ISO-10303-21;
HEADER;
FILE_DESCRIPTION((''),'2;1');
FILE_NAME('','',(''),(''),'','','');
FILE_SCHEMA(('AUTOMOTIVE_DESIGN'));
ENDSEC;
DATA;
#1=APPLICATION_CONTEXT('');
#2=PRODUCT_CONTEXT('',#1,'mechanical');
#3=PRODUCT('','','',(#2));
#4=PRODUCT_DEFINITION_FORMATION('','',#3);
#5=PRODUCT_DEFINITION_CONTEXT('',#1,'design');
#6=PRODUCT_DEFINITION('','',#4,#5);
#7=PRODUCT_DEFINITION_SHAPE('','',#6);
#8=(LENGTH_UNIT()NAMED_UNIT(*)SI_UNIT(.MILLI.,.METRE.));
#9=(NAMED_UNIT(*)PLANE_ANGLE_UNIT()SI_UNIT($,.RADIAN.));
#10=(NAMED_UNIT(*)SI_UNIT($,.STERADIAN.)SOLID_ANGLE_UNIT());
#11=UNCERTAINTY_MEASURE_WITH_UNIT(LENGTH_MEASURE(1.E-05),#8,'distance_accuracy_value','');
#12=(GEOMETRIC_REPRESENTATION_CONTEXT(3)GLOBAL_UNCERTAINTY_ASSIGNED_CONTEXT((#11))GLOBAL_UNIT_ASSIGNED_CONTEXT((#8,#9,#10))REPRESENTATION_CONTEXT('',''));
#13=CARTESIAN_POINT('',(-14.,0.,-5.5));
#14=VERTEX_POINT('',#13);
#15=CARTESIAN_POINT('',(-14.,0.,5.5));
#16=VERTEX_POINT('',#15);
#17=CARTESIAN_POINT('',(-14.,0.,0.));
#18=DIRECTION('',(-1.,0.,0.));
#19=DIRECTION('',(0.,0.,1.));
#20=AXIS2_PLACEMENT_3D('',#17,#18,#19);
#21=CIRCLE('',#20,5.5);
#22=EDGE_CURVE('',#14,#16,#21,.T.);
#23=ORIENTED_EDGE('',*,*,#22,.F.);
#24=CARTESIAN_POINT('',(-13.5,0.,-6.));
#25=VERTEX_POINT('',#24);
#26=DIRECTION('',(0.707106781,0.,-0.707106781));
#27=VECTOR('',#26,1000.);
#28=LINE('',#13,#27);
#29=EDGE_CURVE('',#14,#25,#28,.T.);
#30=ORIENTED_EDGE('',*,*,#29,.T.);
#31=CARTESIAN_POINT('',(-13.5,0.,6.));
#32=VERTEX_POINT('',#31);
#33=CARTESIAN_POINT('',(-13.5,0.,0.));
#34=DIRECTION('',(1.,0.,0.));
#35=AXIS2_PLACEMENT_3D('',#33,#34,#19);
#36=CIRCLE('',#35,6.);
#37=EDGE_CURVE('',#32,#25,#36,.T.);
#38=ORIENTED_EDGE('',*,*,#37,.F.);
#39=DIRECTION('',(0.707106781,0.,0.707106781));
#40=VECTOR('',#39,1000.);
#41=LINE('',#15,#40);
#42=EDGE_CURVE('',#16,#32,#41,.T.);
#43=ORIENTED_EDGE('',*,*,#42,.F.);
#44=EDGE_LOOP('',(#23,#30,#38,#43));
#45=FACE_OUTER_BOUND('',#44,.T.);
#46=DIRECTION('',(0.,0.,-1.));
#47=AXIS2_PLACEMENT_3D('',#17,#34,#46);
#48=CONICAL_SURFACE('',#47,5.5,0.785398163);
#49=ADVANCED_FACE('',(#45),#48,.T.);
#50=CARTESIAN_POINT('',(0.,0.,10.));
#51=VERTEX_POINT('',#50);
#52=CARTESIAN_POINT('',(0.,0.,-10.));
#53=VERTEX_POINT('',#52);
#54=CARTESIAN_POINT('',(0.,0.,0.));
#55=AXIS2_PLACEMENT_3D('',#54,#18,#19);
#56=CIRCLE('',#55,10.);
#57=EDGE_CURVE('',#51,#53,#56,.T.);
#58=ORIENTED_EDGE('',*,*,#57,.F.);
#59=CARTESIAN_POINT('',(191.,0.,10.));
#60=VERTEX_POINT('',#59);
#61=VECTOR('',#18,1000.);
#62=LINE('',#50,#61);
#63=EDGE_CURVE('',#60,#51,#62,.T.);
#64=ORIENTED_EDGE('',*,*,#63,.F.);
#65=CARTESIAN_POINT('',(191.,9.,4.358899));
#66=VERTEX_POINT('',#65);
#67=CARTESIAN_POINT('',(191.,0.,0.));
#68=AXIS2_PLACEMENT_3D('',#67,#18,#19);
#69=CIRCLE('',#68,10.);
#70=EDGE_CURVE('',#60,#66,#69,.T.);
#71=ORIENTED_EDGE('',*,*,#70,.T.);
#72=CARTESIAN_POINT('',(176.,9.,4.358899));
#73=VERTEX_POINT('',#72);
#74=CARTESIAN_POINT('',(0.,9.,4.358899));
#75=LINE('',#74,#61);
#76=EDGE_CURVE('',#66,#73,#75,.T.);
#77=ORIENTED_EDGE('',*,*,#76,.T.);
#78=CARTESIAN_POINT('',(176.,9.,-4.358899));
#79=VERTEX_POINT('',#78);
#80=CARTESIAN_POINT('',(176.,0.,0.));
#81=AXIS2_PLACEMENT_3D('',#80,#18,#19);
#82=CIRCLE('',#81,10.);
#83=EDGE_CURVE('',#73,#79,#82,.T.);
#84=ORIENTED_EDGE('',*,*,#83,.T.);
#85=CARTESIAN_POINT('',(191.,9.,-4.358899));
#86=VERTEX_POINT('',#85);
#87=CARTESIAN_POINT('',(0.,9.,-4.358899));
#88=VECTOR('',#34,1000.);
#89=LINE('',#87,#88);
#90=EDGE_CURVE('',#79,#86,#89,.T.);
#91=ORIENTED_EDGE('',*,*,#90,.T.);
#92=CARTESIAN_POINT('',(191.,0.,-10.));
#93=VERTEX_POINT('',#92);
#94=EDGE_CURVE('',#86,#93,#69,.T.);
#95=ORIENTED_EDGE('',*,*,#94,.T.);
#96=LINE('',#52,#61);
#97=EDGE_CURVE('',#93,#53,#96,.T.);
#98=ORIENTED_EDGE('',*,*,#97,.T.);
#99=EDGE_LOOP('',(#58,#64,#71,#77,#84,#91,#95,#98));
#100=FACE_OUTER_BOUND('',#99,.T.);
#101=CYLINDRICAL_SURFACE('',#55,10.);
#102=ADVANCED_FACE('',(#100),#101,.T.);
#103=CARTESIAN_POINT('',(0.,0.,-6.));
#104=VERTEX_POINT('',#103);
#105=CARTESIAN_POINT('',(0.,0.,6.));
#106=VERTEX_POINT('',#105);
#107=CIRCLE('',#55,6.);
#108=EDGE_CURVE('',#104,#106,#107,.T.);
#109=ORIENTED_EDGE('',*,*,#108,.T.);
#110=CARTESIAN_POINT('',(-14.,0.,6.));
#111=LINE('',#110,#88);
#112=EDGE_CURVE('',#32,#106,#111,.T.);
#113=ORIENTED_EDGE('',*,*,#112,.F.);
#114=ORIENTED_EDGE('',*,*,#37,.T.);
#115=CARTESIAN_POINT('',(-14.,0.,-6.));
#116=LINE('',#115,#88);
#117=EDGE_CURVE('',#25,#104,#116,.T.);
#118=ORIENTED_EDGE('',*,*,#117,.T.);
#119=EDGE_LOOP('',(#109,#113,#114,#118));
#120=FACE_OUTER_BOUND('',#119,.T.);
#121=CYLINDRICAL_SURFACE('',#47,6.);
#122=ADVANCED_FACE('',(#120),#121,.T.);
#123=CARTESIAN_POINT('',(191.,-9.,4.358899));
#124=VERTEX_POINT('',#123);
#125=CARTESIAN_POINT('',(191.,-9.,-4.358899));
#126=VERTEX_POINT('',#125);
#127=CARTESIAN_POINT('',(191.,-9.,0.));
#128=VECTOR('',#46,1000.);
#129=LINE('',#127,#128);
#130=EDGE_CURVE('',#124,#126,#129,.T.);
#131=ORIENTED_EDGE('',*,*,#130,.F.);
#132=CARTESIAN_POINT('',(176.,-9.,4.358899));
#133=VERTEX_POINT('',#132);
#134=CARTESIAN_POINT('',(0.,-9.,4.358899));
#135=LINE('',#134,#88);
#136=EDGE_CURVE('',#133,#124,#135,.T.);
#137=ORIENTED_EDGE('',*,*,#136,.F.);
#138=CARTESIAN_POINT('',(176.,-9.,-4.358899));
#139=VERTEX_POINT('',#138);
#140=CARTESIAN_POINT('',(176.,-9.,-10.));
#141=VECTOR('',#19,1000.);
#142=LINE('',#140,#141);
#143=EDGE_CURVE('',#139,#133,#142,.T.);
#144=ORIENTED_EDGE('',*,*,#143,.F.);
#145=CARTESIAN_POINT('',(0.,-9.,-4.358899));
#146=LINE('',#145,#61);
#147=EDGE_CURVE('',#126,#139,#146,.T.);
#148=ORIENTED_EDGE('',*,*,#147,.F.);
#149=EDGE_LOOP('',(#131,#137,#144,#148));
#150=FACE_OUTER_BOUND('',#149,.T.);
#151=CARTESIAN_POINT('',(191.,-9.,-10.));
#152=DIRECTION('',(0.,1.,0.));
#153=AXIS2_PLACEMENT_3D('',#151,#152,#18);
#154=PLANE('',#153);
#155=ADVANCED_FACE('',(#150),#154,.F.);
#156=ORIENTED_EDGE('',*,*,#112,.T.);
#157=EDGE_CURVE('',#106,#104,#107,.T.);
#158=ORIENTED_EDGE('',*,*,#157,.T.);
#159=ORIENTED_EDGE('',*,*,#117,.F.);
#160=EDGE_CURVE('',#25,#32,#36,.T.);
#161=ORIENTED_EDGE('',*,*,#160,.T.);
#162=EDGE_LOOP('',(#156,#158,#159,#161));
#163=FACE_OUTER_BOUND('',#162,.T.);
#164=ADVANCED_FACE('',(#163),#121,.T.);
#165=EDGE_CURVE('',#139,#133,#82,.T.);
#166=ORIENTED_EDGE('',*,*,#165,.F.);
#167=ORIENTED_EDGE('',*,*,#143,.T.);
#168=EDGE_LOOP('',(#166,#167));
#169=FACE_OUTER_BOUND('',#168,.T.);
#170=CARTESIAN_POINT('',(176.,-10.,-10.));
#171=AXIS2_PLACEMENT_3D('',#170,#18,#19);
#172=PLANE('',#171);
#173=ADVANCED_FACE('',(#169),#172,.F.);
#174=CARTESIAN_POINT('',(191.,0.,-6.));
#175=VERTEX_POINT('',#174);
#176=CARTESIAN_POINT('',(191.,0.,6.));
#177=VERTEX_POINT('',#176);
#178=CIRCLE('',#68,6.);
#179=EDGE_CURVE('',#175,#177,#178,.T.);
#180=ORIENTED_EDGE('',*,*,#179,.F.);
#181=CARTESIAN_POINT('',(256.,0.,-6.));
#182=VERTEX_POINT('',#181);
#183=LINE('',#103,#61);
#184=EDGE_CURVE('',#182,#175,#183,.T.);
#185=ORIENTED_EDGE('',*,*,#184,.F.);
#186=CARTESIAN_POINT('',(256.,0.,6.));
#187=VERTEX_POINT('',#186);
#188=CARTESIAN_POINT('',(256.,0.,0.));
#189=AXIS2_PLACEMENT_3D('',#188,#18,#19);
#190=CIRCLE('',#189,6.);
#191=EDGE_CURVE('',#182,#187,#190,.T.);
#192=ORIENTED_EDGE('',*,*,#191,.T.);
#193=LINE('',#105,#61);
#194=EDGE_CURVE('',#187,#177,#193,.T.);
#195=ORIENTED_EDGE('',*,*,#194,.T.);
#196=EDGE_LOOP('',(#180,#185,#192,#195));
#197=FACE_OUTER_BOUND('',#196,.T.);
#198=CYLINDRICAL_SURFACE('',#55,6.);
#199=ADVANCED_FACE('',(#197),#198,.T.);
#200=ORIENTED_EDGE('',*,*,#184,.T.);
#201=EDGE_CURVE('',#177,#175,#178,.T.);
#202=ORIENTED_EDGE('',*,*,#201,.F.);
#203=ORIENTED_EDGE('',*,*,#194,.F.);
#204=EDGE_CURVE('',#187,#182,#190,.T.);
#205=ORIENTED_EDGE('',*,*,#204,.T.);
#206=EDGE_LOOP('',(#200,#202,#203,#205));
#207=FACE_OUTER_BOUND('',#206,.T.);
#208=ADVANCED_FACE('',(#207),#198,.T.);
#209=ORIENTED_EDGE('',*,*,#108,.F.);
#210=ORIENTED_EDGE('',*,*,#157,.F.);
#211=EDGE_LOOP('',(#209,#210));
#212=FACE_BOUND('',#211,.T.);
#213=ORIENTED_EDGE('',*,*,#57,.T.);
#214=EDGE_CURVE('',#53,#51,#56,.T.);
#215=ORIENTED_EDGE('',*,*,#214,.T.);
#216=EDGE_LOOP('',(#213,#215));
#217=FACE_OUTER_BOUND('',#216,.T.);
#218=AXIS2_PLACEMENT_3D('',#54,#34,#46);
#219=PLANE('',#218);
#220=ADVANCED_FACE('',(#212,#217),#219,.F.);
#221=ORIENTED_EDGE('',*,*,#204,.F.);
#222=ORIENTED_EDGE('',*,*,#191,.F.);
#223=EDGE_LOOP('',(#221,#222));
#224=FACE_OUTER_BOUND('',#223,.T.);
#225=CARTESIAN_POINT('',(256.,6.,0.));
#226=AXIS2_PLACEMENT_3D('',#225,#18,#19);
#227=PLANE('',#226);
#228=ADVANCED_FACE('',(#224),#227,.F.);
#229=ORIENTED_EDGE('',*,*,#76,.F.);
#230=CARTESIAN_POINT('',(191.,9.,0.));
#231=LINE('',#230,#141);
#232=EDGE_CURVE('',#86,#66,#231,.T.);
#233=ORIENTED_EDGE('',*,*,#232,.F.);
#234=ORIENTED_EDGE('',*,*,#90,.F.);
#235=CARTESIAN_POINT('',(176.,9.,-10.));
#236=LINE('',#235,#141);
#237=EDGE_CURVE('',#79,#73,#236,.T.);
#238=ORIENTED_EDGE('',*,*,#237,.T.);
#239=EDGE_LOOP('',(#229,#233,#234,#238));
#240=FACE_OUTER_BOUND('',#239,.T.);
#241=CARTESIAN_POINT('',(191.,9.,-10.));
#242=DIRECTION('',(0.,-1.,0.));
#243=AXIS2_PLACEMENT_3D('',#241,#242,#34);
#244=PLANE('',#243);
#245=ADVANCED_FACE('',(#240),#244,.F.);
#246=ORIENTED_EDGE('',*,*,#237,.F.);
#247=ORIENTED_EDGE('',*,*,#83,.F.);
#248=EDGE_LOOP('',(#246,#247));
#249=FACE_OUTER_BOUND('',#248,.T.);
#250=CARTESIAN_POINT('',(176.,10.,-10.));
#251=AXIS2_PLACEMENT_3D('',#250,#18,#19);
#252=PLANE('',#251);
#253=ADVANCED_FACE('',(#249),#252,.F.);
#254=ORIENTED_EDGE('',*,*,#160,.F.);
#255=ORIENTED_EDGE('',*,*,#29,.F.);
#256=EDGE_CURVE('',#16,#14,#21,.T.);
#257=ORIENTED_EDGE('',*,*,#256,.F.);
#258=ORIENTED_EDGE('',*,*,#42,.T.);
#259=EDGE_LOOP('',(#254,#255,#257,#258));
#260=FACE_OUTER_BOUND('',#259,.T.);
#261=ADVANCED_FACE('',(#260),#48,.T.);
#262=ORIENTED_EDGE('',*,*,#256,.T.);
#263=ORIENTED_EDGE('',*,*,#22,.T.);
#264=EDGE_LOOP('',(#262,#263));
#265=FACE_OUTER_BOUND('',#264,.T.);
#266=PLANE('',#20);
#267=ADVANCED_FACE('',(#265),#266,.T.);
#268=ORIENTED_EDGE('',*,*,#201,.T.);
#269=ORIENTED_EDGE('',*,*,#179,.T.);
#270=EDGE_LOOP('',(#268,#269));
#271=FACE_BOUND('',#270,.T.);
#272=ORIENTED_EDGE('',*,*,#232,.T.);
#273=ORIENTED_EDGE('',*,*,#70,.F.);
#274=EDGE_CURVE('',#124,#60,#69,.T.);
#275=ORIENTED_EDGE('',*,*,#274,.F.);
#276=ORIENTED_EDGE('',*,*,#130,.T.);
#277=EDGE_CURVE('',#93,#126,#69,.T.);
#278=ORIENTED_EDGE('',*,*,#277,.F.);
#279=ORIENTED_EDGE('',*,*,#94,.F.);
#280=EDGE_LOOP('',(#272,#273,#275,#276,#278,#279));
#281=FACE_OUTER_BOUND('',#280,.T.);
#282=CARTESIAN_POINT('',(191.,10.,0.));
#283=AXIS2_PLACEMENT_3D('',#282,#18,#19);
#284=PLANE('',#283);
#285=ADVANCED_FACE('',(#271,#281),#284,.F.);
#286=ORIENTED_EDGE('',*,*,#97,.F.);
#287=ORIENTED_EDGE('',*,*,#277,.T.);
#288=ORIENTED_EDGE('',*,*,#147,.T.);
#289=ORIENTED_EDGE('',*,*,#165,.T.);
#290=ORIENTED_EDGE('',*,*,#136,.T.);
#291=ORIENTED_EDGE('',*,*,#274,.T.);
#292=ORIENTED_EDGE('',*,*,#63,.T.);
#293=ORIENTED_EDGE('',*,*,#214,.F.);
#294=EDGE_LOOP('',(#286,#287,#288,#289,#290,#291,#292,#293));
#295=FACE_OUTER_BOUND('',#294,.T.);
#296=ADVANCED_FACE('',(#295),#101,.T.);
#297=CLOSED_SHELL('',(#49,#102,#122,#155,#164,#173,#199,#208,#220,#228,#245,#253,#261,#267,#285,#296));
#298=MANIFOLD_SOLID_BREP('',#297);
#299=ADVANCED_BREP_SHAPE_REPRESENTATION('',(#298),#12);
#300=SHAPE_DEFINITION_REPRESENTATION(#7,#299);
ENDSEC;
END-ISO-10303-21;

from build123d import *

# Parameters (mm, degrees)
SKETCH6_R           = 6
BOSS_EXTRUDE1_DEPTH = 14
CHAMFER1_SIZE       = 0.5
SKETCH7_W           = 15
SKETCH7_H           = 1
CUT_EXTRUDE1_DEPTH  = 10


with BuildPart() as part:
    # Sketch1 → Revolve1 (revolve)
    with BuildSketch(Plane.XY, mode=Mode.PRIVATE) as revolve1_sk:
        Polygon((0, 0), (0, 10), (191, 10), (191, 6), (256, 6), (256, 0), align=None)
    revolve(revolve1_sk.sketch.rotate(Axis((0, 0, 0), (1, 0, 0)), 90), axis=Axis((0, 0, 0), (1, 0, 0)))

    # Sketch6 → Boss-Extrude1 (add)
    with BuildSketch(Plane.ZY):
        Circle(SKETCH6_R)
    extrude(amount=BOSS_EXTRUDE1_DEPTH)

    # Chamfer1
    chamfer1_edges = [part.edges().sort_by_distance(p)[0] for p in [
        (-14, 0, -6),
    ]]
    chamfer(chamfer1_edges, length=CHAMFER1_SIZE)

    # Sketch7 → Cut-Extrude1 (cut, symmetric)
    with BuildSketch(Plane.XY):
        with Locations((183.5, 9.5)):
            Rectangle(SKETCH7_W, SKETCH7_H)
        with Locations((183.5, -9.5)):
            Rectangle(SKETCH7_W, SKETCH7_H)
    extrude(amount=CUT_EXTRUDE1_DEPTH, both=True, mode=Mode.SUBTRACT)


solid = part.part
